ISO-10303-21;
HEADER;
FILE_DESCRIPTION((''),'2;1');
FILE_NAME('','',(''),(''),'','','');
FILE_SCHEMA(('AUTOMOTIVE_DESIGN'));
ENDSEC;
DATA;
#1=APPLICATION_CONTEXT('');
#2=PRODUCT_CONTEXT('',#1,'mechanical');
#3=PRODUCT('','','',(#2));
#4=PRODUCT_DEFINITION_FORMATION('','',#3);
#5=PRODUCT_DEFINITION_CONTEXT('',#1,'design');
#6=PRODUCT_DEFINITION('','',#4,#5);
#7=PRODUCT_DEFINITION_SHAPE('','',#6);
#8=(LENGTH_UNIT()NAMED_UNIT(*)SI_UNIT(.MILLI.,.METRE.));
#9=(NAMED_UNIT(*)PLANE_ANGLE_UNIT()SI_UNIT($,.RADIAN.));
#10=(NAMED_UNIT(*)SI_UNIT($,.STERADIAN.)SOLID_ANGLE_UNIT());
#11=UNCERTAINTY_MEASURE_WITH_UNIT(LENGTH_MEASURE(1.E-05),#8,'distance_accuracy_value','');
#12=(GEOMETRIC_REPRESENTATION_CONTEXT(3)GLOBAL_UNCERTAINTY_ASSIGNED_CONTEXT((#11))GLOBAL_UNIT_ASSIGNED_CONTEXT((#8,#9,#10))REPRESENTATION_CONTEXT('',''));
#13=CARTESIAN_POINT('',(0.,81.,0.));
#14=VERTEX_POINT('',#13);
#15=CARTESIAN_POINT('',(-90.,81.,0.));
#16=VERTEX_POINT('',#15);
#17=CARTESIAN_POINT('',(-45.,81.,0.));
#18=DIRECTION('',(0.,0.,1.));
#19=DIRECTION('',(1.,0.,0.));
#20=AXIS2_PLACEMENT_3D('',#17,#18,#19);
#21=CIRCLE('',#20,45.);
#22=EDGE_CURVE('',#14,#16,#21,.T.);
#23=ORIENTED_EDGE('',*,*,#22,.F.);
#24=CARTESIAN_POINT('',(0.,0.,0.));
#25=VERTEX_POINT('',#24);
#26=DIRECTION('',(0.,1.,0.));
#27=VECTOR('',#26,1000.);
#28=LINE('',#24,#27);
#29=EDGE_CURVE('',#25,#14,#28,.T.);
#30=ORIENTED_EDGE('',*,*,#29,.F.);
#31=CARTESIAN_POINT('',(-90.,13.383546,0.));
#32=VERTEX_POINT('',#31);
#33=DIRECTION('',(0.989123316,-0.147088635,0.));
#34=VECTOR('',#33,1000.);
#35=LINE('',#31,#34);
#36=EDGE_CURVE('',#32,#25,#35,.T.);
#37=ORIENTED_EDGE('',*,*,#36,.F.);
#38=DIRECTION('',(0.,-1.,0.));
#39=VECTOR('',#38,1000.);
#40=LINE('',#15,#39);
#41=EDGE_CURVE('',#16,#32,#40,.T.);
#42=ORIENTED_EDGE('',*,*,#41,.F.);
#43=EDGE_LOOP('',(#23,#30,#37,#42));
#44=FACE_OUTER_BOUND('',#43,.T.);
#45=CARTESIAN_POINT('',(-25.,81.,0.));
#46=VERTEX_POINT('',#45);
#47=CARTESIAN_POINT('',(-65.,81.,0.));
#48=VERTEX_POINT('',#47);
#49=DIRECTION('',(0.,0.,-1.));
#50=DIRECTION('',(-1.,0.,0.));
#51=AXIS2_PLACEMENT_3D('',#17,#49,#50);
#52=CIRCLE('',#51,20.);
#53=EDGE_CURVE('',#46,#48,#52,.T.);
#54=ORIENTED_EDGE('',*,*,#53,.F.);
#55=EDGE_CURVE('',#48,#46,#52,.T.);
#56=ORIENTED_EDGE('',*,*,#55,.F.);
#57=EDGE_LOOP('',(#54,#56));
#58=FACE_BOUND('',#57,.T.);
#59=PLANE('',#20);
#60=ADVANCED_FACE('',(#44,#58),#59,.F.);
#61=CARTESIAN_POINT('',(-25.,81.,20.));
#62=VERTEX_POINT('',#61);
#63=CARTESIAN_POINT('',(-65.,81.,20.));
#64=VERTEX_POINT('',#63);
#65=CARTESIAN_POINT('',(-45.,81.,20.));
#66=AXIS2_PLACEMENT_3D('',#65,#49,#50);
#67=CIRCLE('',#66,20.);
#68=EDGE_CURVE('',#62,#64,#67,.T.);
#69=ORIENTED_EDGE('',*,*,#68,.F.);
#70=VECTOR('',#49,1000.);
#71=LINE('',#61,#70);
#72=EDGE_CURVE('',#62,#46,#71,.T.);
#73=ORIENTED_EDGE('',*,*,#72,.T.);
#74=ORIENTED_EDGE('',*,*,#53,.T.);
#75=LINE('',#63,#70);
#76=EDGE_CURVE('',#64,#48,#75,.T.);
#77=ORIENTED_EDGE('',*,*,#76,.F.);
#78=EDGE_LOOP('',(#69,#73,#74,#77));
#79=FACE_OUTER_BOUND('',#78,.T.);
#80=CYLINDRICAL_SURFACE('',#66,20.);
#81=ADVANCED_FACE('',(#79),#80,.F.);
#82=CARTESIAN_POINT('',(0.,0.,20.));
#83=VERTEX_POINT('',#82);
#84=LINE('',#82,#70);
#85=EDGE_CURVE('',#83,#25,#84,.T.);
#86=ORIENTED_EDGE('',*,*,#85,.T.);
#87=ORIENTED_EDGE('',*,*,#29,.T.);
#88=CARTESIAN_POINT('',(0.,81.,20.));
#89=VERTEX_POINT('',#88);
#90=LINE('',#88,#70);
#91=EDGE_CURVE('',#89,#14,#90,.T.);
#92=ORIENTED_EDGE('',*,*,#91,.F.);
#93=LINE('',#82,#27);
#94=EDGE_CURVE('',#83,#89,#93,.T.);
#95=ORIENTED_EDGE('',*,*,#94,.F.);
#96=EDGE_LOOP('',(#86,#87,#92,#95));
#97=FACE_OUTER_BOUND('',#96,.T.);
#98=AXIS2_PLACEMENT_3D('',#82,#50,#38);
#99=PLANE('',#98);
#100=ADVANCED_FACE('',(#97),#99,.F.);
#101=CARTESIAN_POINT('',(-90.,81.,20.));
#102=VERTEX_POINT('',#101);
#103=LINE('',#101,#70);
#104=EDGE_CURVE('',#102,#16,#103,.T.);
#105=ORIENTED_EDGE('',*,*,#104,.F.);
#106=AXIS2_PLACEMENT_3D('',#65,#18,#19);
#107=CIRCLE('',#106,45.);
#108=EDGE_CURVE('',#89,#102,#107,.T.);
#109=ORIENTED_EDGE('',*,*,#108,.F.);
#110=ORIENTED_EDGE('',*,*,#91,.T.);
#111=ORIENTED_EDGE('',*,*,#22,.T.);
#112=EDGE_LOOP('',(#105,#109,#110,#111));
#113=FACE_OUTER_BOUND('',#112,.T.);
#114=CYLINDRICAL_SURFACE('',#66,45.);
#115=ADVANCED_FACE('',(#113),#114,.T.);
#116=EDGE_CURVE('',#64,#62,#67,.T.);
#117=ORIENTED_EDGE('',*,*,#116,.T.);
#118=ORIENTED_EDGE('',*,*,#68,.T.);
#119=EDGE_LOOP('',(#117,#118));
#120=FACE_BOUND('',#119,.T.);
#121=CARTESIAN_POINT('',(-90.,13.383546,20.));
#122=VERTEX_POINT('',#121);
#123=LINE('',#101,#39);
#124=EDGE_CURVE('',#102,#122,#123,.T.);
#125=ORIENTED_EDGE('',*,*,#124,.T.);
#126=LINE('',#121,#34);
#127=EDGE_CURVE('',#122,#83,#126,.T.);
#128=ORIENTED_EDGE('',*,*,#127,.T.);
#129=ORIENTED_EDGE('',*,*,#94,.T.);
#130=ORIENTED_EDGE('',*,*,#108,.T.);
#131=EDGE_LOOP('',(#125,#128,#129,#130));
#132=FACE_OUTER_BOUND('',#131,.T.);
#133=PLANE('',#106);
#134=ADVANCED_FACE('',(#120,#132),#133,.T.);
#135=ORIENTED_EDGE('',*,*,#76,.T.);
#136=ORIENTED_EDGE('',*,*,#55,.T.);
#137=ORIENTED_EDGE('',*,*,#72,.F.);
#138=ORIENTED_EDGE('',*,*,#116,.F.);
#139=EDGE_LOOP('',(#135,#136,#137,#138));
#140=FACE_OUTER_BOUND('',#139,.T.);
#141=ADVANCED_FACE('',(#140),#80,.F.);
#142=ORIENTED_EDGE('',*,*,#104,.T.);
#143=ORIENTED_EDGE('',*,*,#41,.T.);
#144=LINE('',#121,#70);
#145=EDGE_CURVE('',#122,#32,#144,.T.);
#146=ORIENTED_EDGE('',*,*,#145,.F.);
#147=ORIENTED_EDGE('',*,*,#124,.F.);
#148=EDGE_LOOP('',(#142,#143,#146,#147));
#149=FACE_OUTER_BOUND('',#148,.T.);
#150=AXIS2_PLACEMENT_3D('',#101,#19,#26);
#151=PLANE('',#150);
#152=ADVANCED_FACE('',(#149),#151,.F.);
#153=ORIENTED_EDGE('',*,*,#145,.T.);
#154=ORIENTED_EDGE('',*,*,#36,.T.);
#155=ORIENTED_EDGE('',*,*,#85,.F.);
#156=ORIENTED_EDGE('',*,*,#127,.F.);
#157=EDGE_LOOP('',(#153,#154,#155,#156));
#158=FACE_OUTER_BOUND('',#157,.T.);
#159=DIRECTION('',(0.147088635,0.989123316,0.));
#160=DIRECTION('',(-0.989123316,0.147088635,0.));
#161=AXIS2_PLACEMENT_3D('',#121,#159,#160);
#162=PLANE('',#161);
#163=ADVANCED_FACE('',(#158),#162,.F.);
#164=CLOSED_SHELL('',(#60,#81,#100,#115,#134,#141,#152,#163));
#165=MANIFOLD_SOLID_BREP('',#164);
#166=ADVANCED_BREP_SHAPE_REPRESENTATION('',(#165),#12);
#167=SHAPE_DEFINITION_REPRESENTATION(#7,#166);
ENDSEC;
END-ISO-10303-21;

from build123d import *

# Parameters (mm, degrees)
EXTRUDE_1_DEPTH     = 20
SKETCH_2_R          = 20
CUT_EXTRUDE_1_DEPTH = 157.12815249


with BuildPart() as part:
    # 草图1 → 凸台-拉伸1 (new body)
    with BuildSketch(Plane.XY):
        with BuildLine():
            Line((0, 0), (0, 81))
            ThreePointArc((0, 81), (-45, 126), (-90, 81))
            Line((-90, 81), (-90, 13.383545734))
            Line((-90, 13.383545734), (0, 0))
        make_face()
    extrude(amount=EXTRUDE_1_DEPTH)

    # 草图2 → 切除-拉伸1 (cut, through all)
    with BuildSketch(Plane(origin=(0, 0, 0), x_dir=(-1, 0, 0), z_dir=(0, 0, -1))):
        with Locations((45, 81)):
            Circle(SKETCH_2_R)
    extrude(amount=-CUT_EXTRUDE_1_DEPTH, mode=Mode.SUBTRACT)


solid = part.part
